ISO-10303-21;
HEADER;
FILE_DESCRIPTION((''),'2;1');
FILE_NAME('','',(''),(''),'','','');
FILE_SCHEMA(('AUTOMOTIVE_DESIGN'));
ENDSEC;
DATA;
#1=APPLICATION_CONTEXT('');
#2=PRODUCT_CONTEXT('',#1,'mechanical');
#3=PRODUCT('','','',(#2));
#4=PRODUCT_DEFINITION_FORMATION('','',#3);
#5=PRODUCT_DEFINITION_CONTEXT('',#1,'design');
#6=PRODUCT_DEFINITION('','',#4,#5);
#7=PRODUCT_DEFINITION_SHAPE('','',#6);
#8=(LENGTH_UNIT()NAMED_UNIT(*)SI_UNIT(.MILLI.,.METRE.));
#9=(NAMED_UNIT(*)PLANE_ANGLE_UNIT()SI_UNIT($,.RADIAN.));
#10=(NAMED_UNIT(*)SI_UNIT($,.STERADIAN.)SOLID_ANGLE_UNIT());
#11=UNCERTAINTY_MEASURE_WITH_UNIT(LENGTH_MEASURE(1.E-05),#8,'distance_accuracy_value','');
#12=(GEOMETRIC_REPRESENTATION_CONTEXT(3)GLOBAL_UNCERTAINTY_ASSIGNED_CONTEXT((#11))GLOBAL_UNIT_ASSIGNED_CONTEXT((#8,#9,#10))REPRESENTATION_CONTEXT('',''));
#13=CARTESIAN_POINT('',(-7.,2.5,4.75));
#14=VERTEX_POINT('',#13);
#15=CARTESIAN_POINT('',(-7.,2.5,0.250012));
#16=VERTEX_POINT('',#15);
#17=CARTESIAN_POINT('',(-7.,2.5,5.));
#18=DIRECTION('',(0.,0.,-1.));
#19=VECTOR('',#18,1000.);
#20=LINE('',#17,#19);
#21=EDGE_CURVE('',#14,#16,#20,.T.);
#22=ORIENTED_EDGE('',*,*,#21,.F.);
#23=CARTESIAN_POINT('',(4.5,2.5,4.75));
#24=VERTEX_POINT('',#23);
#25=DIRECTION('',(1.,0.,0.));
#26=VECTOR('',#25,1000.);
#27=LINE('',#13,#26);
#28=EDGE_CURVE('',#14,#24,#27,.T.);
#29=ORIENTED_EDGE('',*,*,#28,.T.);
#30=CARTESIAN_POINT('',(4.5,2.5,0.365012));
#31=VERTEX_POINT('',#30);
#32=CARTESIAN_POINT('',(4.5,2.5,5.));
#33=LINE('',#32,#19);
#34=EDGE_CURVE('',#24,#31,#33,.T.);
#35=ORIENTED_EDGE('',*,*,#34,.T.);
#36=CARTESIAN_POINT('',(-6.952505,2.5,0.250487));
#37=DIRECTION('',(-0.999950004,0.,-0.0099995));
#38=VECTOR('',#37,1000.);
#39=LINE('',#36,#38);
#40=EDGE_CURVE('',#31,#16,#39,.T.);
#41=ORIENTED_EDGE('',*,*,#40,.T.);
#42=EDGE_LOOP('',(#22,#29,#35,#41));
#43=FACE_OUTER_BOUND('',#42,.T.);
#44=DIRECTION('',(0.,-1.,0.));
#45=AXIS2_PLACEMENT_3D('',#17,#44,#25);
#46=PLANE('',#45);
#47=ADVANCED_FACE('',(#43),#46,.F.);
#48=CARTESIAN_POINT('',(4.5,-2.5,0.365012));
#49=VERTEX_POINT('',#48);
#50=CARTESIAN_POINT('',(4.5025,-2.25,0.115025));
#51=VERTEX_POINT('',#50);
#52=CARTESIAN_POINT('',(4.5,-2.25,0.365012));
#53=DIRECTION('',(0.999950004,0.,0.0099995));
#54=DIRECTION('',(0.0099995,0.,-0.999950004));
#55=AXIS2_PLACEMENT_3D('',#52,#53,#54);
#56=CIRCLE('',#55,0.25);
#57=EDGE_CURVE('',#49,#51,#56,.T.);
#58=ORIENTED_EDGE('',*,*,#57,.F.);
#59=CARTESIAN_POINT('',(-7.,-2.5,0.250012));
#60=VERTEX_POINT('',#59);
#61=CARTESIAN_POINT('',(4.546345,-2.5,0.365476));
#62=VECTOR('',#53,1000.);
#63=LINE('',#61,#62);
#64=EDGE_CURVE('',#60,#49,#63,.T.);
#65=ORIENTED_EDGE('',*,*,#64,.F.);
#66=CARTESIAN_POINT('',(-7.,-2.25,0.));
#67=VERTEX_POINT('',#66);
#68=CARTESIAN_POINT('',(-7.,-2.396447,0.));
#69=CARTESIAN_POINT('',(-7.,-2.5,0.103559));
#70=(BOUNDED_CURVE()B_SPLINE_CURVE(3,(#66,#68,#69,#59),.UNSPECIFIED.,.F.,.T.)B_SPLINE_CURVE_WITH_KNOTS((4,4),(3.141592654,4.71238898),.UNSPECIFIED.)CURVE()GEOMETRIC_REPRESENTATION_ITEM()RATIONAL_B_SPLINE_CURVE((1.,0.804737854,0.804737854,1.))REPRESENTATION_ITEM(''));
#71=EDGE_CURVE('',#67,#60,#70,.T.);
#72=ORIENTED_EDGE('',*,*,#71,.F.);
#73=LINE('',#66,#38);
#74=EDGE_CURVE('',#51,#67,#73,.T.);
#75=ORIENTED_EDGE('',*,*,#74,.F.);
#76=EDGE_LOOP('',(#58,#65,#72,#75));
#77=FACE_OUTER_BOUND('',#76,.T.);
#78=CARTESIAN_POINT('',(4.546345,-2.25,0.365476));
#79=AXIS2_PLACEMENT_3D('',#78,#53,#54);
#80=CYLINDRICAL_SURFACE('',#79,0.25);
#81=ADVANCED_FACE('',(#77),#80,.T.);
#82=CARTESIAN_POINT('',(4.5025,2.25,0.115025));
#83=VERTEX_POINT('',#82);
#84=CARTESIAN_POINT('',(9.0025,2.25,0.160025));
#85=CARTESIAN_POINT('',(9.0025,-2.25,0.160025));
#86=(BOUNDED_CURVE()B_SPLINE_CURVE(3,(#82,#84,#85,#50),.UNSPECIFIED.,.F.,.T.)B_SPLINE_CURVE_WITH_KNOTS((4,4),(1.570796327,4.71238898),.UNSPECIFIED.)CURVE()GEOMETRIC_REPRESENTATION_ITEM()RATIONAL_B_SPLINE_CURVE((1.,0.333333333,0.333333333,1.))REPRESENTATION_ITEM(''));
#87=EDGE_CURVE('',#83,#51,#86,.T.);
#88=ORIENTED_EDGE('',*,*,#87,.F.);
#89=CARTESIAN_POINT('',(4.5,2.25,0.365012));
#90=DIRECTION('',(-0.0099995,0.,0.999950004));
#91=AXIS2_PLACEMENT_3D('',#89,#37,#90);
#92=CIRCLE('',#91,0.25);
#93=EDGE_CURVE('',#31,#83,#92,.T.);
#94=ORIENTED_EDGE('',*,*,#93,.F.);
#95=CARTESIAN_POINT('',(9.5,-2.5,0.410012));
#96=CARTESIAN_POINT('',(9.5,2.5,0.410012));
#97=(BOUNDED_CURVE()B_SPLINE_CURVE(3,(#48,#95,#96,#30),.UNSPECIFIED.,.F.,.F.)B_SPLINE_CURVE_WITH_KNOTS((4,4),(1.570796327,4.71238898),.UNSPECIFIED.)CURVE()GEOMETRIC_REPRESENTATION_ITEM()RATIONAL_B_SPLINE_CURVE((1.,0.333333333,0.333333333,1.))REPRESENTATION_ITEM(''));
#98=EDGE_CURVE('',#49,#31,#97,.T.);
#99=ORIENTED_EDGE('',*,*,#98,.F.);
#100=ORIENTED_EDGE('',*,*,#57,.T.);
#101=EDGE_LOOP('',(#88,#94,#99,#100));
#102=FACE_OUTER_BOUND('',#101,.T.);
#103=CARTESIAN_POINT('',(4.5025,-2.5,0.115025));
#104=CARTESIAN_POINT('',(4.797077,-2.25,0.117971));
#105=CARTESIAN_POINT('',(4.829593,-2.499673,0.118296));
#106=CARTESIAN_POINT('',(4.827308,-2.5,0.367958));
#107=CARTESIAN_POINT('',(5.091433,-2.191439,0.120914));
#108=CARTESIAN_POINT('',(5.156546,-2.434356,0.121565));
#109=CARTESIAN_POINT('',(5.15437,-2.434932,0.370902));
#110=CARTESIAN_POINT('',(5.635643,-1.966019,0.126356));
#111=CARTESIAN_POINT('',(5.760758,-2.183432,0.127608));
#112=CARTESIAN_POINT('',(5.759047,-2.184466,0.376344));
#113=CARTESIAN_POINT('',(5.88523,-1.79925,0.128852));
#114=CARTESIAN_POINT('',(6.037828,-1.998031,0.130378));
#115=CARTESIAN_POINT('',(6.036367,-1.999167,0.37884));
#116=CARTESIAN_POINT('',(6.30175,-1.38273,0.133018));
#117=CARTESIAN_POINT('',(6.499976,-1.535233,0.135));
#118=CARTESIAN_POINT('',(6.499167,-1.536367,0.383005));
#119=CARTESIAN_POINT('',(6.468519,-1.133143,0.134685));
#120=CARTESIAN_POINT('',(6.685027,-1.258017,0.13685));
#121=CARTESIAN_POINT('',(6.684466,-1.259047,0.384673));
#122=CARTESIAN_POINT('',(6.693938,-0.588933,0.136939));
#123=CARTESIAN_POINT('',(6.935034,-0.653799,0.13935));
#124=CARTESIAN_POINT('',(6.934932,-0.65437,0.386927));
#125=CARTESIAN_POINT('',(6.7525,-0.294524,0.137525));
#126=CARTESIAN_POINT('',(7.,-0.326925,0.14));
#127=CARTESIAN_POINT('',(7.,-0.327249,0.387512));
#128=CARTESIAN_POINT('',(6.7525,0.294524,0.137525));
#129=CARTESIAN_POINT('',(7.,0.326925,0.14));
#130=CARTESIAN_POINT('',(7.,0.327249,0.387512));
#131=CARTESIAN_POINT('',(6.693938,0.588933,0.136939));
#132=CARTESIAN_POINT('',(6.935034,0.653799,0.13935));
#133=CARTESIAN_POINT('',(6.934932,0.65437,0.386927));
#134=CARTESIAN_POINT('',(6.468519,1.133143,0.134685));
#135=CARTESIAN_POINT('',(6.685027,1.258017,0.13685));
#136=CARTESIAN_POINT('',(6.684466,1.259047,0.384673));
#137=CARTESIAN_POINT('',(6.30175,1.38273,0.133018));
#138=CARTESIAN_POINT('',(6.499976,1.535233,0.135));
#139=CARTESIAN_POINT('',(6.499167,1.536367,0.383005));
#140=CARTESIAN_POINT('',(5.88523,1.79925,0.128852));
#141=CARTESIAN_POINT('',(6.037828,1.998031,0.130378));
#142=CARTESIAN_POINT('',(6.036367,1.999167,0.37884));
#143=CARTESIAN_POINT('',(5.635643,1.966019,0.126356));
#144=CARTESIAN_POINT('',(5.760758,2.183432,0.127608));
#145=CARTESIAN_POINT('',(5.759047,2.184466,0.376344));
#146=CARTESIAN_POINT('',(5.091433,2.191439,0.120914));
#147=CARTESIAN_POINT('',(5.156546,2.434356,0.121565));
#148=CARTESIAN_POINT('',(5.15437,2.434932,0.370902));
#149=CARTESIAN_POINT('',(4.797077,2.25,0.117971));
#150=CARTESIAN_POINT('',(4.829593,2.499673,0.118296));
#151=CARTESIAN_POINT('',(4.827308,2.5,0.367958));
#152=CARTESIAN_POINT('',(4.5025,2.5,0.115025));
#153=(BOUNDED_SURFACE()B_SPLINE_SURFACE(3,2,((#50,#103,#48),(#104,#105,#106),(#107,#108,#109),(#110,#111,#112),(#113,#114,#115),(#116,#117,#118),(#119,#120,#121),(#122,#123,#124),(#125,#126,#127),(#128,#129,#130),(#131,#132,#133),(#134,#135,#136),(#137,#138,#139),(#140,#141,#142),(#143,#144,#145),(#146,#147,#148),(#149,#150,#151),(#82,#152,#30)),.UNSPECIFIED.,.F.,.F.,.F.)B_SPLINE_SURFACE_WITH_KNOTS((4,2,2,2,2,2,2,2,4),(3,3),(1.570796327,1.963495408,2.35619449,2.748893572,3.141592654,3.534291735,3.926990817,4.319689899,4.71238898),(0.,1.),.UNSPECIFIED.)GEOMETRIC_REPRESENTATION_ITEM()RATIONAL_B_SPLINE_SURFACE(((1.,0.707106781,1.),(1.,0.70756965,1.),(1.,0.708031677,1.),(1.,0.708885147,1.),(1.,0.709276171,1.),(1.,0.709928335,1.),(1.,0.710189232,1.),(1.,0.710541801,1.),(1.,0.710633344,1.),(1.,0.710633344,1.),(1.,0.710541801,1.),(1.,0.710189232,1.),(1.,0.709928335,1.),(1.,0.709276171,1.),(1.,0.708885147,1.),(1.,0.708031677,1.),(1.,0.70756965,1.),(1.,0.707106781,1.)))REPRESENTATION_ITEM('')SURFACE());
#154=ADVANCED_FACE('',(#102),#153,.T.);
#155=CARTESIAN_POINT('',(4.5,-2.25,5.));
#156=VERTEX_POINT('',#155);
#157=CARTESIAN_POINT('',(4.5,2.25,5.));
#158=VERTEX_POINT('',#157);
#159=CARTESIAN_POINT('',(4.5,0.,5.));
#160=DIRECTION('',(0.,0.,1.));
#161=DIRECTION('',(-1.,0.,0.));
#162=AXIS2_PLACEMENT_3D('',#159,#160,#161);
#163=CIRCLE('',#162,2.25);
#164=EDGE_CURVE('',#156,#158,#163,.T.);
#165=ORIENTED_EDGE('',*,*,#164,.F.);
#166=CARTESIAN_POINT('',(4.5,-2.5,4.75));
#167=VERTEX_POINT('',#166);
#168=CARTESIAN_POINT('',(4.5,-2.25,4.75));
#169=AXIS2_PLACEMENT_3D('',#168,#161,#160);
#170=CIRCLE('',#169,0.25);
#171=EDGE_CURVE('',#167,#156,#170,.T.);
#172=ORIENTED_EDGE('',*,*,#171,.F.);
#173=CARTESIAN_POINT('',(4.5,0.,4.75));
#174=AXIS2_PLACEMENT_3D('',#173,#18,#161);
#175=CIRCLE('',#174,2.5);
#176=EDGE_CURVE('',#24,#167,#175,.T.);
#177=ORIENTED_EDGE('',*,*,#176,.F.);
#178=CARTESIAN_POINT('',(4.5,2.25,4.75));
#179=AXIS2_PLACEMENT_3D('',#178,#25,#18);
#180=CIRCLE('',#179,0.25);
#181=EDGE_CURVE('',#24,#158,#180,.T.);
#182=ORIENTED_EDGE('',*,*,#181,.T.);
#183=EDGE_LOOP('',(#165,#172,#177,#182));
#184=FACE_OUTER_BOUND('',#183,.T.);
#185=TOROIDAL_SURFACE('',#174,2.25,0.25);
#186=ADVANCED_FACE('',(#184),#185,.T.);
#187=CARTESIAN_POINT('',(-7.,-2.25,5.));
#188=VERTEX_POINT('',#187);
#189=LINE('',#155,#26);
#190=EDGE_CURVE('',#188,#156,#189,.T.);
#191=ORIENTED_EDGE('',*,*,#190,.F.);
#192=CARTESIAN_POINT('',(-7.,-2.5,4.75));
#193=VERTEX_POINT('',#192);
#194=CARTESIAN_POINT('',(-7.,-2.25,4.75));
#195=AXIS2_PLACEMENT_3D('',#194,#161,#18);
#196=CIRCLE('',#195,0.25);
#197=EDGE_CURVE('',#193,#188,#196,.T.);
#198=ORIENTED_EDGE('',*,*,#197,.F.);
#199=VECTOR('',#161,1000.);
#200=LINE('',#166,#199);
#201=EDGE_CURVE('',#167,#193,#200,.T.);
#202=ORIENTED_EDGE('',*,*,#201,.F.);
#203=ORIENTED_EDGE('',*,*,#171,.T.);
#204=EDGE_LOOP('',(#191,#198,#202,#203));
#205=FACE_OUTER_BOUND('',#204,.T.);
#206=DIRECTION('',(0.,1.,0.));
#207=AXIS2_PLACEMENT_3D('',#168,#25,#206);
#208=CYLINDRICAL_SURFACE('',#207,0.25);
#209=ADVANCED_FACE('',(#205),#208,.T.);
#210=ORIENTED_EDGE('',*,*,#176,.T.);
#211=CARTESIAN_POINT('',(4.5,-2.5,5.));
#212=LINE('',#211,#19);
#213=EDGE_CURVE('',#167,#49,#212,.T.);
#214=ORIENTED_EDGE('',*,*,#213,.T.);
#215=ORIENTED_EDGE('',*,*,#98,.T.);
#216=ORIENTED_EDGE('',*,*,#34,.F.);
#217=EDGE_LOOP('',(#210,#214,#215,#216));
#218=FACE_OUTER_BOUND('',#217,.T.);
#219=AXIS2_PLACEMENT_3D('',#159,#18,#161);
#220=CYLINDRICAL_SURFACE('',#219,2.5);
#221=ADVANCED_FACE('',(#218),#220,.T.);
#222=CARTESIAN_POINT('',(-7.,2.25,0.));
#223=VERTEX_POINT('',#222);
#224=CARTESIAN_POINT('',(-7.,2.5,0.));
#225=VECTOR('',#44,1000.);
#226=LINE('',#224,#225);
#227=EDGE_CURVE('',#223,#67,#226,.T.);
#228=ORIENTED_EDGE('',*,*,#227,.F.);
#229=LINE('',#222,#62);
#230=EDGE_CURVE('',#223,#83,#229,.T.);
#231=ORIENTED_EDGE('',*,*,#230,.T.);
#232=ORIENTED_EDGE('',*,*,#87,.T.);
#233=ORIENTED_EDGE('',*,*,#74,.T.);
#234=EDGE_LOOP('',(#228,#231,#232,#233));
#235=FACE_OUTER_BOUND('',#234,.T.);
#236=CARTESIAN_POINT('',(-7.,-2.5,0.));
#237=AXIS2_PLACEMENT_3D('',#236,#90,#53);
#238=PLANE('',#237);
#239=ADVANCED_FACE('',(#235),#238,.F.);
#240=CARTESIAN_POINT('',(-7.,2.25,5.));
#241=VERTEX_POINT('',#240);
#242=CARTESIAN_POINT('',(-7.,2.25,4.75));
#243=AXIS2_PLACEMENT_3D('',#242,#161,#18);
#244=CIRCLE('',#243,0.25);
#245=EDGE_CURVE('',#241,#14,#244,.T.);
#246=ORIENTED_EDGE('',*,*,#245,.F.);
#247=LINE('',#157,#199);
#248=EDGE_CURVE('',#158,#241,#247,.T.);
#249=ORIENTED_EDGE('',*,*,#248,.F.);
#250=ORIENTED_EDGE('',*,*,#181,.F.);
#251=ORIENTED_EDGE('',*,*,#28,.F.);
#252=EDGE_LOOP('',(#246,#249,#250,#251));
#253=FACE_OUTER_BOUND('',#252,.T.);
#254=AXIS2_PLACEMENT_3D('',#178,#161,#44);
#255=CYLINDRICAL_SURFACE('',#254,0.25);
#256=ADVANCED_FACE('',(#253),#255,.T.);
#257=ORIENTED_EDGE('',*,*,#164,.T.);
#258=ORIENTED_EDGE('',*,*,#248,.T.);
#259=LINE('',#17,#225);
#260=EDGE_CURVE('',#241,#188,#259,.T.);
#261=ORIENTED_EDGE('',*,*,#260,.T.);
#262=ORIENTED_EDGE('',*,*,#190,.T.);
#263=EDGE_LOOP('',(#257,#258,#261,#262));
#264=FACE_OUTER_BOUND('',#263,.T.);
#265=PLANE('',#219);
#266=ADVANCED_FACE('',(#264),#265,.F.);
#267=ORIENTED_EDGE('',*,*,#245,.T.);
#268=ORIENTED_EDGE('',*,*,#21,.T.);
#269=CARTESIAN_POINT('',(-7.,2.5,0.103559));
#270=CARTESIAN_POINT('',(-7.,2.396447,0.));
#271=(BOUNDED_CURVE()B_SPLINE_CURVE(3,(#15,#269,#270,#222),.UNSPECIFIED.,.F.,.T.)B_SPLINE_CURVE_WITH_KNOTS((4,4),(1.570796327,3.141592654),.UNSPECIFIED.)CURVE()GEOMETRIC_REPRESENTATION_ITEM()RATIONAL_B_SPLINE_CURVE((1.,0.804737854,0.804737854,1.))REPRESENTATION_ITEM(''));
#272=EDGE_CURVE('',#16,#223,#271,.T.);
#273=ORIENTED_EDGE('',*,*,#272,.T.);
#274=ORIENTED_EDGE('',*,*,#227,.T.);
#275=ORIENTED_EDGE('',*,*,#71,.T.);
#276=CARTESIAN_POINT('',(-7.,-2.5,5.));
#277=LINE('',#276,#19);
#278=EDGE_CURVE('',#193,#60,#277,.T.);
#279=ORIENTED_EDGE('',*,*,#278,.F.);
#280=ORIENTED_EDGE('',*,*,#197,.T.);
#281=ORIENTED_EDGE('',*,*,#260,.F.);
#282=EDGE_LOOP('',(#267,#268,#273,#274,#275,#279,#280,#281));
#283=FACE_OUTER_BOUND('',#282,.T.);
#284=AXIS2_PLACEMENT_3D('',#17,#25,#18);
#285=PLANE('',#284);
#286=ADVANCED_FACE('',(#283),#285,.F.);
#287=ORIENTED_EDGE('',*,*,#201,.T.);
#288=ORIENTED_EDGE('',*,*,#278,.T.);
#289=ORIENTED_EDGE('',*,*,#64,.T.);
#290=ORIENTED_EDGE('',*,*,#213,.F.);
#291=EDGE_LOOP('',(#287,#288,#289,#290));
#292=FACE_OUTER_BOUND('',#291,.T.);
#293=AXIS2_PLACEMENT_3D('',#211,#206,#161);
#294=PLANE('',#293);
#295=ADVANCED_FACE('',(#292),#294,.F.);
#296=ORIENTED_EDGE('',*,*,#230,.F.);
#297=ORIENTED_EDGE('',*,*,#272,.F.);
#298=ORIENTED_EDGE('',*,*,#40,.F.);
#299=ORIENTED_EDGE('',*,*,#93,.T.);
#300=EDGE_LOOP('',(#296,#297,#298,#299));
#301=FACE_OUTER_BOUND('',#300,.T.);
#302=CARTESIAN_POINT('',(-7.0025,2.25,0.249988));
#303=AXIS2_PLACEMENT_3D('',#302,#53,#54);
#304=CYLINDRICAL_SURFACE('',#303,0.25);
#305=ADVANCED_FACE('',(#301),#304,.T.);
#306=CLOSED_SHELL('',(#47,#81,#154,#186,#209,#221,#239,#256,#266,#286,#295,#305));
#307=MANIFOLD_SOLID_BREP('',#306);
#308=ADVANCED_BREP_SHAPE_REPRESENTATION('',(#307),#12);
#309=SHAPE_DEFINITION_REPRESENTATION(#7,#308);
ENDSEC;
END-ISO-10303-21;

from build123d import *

# Parameters (mm, degrees)
EXTRUDE1_DEPTH          = 5
CUT_EXTRUDE1_DEPTH      = 9.958236434
CUT_EXTRUDE1_DEPTH_BACK = 9.958236434
FILLET2_R               = 0.25


with BuildPart() as part:
    # Sketch1 → Extrude1 (new body)
    with BuildSketch(Plane.XY):
        with BuildLine():
            Line((-7, 2.5), (4.5, 2.5))
            ThreePointArc((4.5, 2.5), (7, 0), (4.5, -2.5))
            Line((4.5, -2.5), (-7, -2.5))
            Line((-7, -2.5), (-7, 2.5))
        make_face()
    extrude(amount=EXTRUDE1_DEPTH)

    # Sketch2 → Cut-Extrude1 (cut, two sides: drawn at the far end of the back side and taken through both)
    with BuildSketch(Plane(origin=(0, 0, 0), x_dir=(1, 0, 0), z_dir=(0, 1, 0)).offset(-CUT_EXTRUDE1_DEPTH_BACK)):
        Polygon((-7, 0), (7, 0), (7, -0.14), align=None)
    extrude(amount=CUT_EXTRUDE1_DEPTH + CUT_EXTRUDE1_DEPTH_BACK, mode=Mode.SUBTRACT)

    # Fillet2
    fillet2_edges = [part.edges().sort_by_distance(p)[0] for p in [
        (7, 0, 5),
        (-1.25, 2.5, 5),
        (-1.25, -2.5, 0.0575),
        (6.267744857, -1.767789049, 0.132677449),
        (-1.25, 2.5, 0.0575),
        (-1.25, -2.5, 5),
    ]]
    fillet(fillet2_edges, radius=FILLET2_R)


solid = part.part
